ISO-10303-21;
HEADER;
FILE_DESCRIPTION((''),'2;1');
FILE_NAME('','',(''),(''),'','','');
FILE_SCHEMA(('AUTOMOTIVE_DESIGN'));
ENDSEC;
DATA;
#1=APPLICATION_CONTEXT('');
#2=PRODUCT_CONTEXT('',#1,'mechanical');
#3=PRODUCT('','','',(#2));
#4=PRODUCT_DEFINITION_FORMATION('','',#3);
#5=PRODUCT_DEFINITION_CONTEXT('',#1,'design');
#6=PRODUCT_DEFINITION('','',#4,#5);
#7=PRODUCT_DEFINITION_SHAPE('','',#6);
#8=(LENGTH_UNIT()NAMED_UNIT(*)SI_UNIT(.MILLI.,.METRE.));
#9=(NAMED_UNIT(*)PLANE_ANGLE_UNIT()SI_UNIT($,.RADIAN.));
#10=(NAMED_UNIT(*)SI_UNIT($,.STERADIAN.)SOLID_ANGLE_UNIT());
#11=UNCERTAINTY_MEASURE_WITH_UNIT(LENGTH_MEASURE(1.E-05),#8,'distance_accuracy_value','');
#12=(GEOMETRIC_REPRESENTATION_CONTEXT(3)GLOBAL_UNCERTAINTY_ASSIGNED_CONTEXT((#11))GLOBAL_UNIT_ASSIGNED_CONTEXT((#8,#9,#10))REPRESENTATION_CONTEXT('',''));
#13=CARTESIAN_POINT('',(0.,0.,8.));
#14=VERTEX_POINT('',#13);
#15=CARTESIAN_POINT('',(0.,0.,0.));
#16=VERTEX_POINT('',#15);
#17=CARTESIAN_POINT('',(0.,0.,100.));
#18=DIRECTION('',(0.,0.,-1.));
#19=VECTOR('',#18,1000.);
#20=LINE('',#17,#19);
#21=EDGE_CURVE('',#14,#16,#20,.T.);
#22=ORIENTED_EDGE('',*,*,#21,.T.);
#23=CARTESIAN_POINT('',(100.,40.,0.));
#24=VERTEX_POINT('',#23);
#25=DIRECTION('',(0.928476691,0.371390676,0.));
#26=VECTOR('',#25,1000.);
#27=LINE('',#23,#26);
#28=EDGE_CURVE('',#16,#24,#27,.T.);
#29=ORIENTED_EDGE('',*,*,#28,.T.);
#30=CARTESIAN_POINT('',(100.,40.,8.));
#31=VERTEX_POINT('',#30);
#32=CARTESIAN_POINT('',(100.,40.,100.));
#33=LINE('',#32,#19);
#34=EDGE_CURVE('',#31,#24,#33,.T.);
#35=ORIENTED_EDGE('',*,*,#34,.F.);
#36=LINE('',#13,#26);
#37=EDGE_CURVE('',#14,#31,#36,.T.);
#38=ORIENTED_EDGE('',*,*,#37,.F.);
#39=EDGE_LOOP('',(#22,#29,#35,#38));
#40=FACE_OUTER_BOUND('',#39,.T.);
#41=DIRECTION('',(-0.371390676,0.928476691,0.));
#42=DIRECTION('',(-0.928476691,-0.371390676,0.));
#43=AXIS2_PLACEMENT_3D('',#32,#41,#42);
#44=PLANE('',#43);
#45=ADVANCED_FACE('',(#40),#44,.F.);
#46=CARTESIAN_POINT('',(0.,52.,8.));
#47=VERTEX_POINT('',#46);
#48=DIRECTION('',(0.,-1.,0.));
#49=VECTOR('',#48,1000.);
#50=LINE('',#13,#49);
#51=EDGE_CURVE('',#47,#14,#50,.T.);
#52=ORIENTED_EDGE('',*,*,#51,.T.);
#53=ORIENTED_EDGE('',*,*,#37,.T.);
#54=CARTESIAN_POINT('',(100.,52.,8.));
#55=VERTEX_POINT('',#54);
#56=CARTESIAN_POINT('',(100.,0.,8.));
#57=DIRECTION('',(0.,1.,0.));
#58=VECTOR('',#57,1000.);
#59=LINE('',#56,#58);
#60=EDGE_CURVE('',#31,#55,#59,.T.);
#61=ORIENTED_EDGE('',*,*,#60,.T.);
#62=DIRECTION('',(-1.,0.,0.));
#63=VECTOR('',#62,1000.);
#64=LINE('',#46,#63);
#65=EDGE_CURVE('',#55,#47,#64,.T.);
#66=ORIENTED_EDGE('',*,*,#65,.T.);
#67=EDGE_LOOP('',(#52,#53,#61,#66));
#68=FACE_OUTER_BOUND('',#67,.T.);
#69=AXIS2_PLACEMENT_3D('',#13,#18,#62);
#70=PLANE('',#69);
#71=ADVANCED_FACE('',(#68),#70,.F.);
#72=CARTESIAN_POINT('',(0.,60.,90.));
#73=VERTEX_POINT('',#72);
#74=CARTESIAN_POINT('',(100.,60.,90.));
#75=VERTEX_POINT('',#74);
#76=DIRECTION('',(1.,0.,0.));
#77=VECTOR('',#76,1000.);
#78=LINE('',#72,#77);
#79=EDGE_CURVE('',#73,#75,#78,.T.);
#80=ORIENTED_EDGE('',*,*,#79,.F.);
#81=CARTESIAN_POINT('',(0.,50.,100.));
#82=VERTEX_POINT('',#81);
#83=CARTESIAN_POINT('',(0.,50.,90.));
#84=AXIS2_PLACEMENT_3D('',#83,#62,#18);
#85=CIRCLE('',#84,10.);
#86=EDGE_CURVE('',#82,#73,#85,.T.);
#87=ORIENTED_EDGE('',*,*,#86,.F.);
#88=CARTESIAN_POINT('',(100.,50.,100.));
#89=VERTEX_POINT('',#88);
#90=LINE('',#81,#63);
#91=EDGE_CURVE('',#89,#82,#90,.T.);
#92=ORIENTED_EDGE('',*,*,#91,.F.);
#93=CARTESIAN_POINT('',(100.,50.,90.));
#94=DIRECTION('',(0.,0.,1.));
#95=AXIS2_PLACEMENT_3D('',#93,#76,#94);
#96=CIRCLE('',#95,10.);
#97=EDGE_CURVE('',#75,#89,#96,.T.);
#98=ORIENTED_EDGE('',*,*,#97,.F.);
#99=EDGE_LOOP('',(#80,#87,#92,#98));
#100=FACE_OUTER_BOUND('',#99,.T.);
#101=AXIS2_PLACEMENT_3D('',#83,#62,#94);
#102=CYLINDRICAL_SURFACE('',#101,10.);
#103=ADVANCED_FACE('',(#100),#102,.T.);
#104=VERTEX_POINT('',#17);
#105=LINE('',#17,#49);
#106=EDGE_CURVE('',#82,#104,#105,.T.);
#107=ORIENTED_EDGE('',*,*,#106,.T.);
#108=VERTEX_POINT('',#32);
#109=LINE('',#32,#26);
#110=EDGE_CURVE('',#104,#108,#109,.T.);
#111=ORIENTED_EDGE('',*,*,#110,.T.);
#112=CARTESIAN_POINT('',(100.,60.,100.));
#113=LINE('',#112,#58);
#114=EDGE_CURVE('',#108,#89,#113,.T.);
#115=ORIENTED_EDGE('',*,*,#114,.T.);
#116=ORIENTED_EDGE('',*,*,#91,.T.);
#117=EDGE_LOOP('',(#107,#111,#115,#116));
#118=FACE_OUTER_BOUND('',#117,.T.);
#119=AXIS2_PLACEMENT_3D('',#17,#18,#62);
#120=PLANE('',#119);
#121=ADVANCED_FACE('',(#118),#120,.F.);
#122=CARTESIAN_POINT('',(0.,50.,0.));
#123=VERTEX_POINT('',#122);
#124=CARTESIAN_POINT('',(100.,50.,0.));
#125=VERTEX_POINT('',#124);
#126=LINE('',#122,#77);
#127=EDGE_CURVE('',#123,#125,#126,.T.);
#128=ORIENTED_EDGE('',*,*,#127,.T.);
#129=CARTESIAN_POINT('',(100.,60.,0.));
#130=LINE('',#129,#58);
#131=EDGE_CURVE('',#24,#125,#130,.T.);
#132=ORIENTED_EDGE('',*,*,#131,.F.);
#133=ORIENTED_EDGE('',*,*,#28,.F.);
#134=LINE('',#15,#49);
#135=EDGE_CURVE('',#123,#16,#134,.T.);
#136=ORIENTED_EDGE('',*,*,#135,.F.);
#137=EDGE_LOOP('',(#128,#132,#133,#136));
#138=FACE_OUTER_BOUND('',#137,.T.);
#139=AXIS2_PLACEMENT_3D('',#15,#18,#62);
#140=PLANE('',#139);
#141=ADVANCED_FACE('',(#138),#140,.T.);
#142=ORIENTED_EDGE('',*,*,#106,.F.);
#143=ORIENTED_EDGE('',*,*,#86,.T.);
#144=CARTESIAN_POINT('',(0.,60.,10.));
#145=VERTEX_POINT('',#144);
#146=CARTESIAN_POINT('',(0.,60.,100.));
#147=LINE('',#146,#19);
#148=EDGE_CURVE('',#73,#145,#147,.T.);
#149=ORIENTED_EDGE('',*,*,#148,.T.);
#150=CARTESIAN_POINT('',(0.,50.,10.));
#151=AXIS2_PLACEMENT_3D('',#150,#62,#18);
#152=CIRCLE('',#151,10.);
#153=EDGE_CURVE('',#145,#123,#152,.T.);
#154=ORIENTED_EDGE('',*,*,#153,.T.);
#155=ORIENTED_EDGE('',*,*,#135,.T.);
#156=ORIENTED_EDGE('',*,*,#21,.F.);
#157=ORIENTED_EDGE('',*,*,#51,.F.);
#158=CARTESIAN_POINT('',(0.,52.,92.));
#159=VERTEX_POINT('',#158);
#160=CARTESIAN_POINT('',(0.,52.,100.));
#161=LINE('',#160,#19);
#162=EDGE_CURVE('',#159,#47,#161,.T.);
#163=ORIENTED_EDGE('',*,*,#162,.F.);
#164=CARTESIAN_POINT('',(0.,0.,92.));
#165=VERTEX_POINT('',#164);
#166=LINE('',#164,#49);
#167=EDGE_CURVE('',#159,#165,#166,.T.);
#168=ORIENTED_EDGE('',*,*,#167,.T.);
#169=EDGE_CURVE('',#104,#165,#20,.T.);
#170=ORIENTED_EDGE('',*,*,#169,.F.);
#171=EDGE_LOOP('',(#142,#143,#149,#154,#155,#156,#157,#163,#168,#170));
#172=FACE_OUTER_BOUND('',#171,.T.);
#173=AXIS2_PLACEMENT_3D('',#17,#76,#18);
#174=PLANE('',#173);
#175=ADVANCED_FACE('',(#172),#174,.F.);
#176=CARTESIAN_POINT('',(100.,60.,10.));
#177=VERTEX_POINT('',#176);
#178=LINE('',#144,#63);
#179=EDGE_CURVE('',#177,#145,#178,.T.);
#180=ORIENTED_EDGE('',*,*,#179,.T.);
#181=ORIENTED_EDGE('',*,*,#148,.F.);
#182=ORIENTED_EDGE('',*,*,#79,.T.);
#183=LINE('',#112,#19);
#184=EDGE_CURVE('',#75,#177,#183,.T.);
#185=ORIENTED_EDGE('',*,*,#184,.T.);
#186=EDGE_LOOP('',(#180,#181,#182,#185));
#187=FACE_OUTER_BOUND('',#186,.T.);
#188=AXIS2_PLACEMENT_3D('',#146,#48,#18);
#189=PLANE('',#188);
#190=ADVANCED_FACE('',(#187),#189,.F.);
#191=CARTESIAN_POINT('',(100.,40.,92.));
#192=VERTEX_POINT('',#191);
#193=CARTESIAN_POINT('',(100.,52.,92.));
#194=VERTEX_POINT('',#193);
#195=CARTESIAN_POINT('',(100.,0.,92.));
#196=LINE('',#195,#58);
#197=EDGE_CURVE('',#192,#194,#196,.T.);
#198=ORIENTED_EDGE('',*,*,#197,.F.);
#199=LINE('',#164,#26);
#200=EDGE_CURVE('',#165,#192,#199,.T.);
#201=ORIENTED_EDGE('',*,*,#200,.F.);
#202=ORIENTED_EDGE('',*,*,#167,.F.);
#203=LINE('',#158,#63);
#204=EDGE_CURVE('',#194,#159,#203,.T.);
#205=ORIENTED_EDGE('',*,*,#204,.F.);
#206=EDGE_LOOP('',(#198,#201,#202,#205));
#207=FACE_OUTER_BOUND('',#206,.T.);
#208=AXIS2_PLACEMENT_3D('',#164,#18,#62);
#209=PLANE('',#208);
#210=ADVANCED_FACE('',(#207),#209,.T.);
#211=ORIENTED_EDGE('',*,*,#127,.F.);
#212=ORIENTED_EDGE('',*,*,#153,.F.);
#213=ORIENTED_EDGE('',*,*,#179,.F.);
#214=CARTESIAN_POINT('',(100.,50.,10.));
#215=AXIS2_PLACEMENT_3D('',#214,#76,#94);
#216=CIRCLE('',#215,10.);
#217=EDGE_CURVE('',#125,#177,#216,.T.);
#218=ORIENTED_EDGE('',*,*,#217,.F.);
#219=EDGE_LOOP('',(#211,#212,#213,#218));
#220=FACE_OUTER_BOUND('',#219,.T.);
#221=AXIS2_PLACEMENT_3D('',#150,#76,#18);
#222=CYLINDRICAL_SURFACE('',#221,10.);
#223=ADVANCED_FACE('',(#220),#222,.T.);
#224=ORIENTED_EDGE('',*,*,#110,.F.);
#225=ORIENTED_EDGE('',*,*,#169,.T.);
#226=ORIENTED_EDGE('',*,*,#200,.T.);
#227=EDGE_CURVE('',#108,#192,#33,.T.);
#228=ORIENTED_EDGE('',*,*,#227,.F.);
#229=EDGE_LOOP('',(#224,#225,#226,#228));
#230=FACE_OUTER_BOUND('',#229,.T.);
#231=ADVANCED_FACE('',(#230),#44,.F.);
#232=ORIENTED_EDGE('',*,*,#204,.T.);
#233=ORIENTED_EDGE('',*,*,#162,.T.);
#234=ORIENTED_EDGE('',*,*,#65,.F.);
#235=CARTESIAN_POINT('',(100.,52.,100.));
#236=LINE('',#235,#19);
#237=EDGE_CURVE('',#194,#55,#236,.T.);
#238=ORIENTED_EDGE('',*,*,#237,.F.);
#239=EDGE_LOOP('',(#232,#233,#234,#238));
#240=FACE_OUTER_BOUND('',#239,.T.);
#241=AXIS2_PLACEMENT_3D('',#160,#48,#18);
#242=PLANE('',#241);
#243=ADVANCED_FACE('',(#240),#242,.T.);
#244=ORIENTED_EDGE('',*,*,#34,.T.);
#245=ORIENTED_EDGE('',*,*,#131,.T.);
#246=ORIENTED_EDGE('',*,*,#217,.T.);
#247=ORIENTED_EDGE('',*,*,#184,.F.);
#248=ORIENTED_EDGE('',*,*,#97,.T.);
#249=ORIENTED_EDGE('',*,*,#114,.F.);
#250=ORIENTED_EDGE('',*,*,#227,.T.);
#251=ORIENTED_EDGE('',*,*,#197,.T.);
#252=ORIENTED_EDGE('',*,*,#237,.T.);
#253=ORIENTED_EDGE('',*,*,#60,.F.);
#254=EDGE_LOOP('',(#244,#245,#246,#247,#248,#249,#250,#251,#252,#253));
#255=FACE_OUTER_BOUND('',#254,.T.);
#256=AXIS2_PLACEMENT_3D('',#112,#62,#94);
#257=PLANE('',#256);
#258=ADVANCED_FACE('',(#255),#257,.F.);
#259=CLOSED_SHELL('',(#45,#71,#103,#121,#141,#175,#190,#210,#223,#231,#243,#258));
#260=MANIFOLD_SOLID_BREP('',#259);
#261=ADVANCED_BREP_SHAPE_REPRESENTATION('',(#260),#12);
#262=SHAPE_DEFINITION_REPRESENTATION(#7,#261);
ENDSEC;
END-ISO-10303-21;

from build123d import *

# Parameters (mm, degrees)
EXTRUDE_1_DEPTH = 100
SHELL_1_T       = -8
FILLET_1_R      = 10
FILLET_2_R      = 10


with BuildPart() as part:
    # 草图1 → 凸台-拉伸1 (new body)
    with BuildSketch(Plane.XY):
        Polygon((0, 0), (0, 60), (100, 60), (100, 40), align=None)
    extrude(amount=EXTRUDE_1_DEPTH)

    # 抽壳1
    shell_1_openings = [part.faces().sort_by_distance(p)[0] for p in [
        (0, 30, 50),
        (100, 50, 50),
        (50, 20, 50),
    ]]
    offset(amount=SHELL_1_T, openings=shell_1_openings, kind=Kind.INTERSECTION)

    # 圆角1
    fillet_1_edges = [part.edges().sort_by_distance(p)[0] for p in [
        (50, 60, 100),
    ]]
    fillet(fillet_1_edges, radius=FILLET_1_R)

    # 圆角2
    fillet_2_edges = [part.edges().sort_by_distance(p)[0] for p in [
        (50, 60, 0),
    ]]
    fillet(fillet_2_edges, radius=FILLET_2_R)


solid = part.part
